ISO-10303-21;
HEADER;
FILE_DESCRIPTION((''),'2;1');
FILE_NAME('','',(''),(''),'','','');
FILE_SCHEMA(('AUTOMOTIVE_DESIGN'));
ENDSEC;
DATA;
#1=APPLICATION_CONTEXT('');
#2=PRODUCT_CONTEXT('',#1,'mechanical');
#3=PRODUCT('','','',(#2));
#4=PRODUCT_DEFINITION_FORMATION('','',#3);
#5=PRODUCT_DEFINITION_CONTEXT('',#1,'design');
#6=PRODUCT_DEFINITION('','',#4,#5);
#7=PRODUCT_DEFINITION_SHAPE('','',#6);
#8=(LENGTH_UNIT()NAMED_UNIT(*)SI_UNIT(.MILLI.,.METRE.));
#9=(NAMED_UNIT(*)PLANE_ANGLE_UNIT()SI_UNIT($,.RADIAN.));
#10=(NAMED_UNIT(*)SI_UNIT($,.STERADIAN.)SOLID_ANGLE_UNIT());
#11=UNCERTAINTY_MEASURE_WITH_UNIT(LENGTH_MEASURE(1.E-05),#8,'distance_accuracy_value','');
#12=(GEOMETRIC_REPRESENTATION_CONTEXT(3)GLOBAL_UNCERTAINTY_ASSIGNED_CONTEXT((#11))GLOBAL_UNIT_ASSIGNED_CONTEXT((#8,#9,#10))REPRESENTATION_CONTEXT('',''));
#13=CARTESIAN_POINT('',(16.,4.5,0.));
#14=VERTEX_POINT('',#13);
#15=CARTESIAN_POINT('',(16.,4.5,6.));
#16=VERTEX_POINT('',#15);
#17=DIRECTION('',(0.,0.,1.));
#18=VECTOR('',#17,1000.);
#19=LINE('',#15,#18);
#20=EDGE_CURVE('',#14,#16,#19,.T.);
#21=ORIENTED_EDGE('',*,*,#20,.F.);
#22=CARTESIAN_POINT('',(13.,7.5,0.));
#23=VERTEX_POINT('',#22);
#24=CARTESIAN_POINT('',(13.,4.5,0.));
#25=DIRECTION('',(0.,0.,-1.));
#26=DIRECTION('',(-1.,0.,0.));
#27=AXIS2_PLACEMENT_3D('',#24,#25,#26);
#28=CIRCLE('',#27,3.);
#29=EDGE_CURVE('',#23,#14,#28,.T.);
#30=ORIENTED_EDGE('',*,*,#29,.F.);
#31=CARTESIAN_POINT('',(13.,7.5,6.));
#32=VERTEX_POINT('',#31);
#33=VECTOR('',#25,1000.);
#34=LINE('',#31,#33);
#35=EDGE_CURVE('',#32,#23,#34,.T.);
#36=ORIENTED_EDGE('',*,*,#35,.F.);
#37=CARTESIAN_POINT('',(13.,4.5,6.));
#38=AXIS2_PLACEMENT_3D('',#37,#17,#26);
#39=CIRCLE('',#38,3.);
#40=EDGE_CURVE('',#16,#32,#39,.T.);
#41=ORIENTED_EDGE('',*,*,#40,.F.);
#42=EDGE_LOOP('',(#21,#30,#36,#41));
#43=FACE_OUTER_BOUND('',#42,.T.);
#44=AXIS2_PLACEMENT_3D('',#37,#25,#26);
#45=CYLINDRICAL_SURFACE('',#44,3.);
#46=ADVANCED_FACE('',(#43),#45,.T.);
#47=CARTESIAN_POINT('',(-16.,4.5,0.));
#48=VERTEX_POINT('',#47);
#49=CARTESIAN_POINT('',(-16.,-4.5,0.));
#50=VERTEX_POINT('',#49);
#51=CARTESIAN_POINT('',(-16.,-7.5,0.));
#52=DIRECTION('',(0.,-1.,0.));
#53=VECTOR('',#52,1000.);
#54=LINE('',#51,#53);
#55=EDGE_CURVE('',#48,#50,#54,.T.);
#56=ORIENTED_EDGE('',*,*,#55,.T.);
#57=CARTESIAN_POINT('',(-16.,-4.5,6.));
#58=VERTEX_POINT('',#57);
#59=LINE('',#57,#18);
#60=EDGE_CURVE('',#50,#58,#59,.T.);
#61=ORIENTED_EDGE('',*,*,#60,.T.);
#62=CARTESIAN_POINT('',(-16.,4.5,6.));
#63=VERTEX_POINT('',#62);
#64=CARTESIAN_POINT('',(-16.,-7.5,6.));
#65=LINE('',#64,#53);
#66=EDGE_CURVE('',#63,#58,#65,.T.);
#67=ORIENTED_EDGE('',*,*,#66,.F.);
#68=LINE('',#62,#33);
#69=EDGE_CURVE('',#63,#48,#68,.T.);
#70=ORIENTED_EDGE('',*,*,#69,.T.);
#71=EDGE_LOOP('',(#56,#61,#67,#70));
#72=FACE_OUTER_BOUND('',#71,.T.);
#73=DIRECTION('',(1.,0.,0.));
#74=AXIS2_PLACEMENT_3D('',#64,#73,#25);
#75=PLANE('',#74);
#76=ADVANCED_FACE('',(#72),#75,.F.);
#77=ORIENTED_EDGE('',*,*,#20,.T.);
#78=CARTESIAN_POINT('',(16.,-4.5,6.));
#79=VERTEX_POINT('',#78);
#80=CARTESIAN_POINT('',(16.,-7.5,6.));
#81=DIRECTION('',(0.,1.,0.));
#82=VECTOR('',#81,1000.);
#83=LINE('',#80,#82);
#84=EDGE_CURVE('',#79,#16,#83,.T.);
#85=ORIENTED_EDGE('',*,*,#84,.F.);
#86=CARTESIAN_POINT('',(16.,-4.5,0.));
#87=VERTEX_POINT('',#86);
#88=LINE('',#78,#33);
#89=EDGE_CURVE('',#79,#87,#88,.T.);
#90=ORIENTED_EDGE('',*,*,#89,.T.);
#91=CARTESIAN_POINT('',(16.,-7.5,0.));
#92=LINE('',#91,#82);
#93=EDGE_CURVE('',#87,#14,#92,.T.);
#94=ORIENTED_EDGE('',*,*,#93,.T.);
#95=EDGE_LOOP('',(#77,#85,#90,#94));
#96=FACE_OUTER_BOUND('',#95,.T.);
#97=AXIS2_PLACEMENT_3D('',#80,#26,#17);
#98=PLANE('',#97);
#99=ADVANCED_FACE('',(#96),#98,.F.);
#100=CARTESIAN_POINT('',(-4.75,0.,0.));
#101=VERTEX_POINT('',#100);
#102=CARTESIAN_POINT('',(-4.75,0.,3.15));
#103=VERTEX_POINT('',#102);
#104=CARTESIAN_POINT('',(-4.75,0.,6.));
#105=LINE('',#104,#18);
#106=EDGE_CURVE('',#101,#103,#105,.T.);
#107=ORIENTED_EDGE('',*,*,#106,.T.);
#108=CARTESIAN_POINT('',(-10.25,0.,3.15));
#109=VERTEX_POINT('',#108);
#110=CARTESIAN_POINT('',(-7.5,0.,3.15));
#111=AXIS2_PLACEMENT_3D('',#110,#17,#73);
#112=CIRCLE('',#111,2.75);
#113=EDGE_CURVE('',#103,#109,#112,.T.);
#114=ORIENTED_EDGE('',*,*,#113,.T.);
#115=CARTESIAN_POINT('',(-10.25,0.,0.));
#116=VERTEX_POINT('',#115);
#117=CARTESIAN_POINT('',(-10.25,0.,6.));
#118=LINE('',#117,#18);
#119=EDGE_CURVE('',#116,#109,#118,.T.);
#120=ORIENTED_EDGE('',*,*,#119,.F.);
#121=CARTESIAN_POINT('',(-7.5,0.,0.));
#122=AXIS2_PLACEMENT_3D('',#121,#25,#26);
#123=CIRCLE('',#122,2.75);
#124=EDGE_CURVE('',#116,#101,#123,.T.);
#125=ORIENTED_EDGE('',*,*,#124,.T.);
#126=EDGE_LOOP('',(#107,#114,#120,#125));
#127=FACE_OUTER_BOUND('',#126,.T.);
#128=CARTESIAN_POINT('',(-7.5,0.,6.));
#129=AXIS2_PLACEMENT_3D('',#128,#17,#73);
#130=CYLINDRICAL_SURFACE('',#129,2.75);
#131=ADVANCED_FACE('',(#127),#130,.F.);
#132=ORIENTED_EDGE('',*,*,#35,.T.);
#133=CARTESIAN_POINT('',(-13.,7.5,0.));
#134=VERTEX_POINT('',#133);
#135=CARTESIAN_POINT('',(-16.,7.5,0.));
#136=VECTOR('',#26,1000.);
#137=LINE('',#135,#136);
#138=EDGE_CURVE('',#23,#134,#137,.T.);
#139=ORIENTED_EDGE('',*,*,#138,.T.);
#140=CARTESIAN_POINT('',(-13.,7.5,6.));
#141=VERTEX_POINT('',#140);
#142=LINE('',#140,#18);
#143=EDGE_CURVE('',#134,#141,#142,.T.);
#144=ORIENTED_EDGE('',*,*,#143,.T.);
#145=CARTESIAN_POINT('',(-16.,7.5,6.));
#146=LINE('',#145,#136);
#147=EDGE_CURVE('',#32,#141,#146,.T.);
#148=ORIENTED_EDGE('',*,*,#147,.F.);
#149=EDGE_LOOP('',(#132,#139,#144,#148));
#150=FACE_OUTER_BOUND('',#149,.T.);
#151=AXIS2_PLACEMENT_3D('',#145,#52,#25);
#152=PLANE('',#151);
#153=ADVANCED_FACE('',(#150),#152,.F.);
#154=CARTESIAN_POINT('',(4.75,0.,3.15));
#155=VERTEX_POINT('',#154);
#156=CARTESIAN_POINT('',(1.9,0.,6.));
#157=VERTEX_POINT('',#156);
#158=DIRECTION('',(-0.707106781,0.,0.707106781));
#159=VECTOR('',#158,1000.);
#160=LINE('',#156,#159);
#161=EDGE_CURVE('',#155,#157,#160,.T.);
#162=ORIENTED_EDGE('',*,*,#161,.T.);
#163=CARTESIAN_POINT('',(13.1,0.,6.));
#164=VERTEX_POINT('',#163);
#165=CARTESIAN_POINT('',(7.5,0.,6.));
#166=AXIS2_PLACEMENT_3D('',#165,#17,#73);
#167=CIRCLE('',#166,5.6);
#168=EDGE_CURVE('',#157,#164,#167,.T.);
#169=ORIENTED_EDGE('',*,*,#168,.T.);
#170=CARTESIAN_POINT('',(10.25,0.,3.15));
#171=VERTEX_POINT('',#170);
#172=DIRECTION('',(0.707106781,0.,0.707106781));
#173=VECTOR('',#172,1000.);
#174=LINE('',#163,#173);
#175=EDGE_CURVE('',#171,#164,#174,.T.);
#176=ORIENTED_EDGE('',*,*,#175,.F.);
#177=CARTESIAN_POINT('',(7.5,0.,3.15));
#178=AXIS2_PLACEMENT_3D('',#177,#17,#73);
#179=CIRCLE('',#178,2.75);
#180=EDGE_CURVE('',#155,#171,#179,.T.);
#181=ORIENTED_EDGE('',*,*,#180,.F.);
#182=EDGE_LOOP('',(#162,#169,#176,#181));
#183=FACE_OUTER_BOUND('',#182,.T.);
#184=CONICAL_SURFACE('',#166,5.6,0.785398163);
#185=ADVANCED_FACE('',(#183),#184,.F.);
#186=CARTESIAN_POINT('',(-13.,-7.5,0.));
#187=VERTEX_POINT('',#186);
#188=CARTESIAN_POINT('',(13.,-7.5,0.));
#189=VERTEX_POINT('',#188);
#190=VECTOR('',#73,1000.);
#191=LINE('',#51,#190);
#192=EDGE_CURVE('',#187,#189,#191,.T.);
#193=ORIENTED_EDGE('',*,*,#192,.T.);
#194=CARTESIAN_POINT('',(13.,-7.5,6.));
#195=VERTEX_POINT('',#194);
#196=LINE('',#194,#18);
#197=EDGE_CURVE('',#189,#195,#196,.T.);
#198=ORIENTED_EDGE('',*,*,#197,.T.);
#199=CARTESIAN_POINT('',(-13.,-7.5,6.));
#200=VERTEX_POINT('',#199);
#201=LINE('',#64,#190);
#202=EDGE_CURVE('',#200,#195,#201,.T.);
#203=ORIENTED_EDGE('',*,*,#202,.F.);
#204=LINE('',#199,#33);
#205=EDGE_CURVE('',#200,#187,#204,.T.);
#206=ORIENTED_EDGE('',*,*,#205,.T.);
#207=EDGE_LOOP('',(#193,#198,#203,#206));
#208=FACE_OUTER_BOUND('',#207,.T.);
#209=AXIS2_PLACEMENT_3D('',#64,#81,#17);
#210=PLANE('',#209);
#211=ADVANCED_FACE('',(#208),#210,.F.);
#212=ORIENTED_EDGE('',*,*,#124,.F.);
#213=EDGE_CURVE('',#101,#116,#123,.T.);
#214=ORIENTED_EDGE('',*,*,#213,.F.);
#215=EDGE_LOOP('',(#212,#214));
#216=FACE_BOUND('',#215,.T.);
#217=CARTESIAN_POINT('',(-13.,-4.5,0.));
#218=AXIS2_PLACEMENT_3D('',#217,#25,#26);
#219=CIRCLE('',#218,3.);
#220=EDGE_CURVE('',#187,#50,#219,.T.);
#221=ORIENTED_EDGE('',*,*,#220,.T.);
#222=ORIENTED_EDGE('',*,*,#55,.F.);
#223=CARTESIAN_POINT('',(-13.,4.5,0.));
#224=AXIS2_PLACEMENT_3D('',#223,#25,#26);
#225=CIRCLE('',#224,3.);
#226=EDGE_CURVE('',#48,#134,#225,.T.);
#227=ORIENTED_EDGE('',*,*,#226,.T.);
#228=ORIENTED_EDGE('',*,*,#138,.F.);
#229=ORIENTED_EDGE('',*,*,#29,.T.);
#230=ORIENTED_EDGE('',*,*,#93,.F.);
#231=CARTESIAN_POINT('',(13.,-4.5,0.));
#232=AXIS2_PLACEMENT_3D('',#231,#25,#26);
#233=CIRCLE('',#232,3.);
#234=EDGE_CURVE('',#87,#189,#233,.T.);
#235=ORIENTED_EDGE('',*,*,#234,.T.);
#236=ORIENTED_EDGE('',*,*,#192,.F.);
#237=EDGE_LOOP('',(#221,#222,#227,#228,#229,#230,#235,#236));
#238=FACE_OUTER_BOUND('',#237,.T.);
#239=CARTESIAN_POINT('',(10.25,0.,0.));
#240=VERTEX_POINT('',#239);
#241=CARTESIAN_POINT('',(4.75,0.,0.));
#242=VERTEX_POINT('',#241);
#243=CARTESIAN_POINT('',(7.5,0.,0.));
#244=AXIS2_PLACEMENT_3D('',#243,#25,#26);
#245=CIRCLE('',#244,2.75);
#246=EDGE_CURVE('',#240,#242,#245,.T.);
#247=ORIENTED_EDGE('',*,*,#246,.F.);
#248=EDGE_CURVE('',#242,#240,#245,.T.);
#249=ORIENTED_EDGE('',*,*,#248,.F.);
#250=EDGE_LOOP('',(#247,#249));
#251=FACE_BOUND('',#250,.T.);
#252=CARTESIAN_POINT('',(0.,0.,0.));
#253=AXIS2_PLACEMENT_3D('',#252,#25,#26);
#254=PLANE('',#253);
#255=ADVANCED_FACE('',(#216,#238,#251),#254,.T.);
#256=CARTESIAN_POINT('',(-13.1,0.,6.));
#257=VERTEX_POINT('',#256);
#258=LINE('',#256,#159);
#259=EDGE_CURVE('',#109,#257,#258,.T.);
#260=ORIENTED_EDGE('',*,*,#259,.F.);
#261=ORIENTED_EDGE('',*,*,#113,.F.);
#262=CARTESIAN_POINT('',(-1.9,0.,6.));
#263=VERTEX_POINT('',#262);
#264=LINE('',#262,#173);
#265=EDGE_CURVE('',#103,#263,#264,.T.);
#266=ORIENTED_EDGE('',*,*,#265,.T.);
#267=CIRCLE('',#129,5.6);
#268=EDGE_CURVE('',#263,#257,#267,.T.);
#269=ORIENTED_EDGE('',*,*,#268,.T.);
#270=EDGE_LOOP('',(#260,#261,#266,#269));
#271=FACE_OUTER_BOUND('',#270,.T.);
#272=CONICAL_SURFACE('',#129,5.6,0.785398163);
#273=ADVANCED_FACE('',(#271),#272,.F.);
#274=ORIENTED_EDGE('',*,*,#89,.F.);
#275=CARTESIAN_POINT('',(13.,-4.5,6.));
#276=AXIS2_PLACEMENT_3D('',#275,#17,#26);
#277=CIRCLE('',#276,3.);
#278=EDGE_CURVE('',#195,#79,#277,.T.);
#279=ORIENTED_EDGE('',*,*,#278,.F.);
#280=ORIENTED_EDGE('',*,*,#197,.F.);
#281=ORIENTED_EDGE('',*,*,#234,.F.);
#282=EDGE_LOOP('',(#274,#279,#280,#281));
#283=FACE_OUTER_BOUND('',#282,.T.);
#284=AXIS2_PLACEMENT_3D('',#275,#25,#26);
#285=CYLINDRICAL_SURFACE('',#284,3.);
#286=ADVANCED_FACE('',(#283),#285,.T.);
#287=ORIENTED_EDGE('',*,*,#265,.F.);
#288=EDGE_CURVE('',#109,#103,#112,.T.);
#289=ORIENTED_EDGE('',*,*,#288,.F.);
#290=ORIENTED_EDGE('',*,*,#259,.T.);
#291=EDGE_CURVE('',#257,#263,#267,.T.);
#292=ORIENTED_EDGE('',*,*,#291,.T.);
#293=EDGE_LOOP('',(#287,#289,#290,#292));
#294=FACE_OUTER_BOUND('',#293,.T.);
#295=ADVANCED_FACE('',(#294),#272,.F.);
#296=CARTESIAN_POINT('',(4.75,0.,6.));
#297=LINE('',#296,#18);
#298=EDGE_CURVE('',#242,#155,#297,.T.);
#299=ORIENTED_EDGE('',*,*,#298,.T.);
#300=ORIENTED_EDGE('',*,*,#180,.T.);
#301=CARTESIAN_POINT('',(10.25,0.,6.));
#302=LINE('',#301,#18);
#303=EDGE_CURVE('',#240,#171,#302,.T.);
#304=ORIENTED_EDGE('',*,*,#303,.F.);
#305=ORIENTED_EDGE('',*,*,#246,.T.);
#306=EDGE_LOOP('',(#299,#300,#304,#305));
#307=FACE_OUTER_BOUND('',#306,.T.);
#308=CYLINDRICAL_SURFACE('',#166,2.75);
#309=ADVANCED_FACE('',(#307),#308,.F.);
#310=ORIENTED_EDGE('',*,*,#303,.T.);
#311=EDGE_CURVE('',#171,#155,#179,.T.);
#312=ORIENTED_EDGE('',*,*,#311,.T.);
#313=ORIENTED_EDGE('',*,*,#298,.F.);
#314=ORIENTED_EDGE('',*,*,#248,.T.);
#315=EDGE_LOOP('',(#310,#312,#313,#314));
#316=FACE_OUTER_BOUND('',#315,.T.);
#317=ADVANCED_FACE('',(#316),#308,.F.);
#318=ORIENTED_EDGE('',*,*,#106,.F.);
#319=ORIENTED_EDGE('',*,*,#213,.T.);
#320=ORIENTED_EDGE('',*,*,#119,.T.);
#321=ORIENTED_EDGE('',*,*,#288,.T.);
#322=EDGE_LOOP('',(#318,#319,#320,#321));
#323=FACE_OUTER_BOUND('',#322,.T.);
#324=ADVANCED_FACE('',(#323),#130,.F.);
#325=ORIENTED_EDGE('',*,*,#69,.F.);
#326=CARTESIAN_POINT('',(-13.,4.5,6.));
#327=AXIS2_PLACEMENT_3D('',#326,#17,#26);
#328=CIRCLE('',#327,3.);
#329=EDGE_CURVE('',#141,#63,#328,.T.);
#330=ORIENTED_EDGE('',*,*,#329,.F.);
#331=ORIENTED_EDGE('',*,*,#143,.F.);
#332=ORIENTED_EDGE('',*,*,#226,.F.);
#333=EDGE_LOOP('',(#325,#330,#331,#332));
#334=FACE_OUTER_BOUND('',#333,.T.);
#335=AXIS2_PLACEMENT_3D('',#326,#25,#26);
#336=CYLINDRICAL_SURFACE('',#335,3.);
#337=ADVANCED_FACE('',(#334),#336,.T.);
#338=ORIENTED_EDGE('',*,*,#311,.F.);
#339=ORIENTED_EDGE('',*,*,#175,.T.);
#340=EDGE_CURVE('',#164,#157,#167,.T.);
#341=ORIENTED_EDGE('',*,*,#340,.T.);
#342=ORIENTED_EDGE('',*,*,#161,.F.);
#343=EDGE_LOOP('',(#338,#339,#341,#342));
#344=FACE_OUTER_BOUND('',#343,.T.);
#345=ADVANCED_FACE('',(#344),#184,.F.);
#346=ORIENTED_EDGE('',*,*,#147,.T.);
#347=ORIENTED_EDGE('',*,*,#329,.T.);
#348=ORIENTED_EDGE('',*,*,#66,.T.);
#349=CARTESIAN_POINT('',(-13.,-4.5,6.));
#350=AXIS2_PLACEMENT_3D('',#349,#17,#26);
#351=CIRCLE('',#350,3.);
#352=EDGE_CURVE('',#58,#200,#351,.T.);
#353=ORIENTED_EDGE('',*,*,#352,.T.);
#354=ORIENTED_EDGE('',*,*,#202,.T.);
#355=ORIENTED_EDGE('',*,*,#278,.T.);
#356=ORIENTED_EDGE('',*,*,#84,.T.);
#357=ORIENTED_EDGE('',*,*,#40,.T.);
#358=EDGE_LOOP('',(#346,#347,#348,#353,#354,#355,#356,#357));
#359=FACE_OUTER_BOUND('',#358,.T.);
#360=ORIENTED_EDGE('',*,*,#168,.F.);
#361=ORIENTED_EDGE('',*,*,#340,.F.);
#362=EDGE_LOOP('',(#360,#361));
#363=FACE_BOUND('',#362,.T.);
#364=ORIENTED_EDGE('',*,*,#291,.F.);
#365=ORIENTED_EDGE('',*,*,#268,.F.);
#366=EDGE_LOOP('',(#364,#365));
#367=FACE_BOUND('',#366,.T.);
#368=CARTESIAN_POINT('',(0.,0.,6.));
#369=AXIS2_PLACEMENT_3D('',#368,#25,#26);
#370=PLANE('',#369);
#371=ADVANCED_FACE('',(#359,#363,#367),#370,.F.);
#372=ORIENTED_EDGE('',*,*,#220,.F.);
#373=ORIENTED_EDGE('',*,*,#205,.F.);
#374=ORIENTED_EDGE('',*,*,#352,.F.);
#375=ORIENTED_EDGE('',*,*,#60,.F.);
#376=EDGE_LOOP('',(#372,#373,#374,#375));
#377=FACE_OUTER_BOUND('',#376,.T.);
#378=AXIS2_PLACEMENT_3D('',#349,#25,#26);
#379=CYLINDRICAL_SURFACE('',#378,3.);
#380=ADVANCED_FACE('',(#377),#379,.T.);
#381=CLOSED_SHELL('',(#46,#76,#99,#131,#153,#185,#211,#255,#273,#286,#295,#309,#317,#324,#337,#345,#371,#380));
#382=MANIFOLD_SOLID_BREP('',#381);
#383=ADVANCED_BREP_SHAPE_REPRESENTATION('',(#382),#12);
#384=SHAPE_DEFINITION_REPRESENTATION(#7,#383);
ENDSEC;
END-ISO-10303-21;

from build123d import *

# Parameters (mm, degrees)
SKETCH1_W                                            = 32
SKETCH1_H                                            = 15
BOSS_EXTRUDE1_DEPTH                                  = 6
CSK_FOR_M5_SLOTTED_RAISED_CTSK_HEAD_WOOD_D           = 5.5
CSK_FOR_M5_SLOTTED_RAISED_CTSK_HEAD_WOOD_DEPTH       = 12.4
CSK_FOR_M5_SLOTTED_RAISED_CTSK_HEAD_WOOD_CSINK_D     = 11.2
CSK_FOR_M5_SLOTTED_RAISED_CTSK_HEAD_WOOD_CSINK_ANGLE = 90
CSK_FOR_M5_SLOTTED_RAISED_CTSK_HEAD_WOOD_TIP         = 1.652366702
FILLET1_R                                            = 3


with BuildPart() as part:
    # Sketch1 → Boss-Extrude1 (new body)
    with BuildSketch(Plane.XY):
        Rectangle(SKETCH1_W, SKETCH1_H)
    extrude(amount=BOSS_EXTRUDE1_DEPTH)

    # CSK for M5 Slotted raised CTSK head wood screws1
    with Locations(Plane.XY.offset(6)):
        with Locations((7.5, 0), (60, 0), (-60, 0), (-7.5, 0)):
            CounterSinkHole(CSK_FOR_M5_SLOTTED_RAISED_CTSK_HEAD_WOOD_D / 2, CSK_FOR_M5_SLOTTED_RAISED_CTSK_HEAD_WOOD_CSINK_D / 2, depth=CSK_FOR_M5_SLOTTED_RAISED_CTSK_HEAD_WOOD_DEPTH, counter_sink_angle=CSK_FOR_M5_SLOTTED_RAISED_CTSK_HEAD_WOOD_CSINK_ANGLE)
            with Locations((0, 0, -(CSK_FOR_M5_SLOTTED_RAISED_CTSK_HEAD_WOOD_DEPTH + CSK_FOR_M5_SLOTTED_RAISED_CTSK_HEAD_WOOD_TIP / 2))):  # 118° drill point
                Cone(0, CSK_FOR_M5_SLOTTED_RAISED_CTSK_HEAD_WOOD_D / 2, CSK_FOR_M5_SLOTTED_RAISED_CTSK_HEAD_WOOD_TIP, mode=Mode.SUBTRACT)

    # Fillet1
    fillet1_edges = [part.edges().sort_by_distance(p)[0] for p in [
        (16, -7.5, 3),
        (-16, -7.5, 3),
        (-16, 7.5, 3),
        (16, 7.5, 3),
    ]]
    fillet(fillet1_edges, radius=FILLET1_R)


solid = part.part
